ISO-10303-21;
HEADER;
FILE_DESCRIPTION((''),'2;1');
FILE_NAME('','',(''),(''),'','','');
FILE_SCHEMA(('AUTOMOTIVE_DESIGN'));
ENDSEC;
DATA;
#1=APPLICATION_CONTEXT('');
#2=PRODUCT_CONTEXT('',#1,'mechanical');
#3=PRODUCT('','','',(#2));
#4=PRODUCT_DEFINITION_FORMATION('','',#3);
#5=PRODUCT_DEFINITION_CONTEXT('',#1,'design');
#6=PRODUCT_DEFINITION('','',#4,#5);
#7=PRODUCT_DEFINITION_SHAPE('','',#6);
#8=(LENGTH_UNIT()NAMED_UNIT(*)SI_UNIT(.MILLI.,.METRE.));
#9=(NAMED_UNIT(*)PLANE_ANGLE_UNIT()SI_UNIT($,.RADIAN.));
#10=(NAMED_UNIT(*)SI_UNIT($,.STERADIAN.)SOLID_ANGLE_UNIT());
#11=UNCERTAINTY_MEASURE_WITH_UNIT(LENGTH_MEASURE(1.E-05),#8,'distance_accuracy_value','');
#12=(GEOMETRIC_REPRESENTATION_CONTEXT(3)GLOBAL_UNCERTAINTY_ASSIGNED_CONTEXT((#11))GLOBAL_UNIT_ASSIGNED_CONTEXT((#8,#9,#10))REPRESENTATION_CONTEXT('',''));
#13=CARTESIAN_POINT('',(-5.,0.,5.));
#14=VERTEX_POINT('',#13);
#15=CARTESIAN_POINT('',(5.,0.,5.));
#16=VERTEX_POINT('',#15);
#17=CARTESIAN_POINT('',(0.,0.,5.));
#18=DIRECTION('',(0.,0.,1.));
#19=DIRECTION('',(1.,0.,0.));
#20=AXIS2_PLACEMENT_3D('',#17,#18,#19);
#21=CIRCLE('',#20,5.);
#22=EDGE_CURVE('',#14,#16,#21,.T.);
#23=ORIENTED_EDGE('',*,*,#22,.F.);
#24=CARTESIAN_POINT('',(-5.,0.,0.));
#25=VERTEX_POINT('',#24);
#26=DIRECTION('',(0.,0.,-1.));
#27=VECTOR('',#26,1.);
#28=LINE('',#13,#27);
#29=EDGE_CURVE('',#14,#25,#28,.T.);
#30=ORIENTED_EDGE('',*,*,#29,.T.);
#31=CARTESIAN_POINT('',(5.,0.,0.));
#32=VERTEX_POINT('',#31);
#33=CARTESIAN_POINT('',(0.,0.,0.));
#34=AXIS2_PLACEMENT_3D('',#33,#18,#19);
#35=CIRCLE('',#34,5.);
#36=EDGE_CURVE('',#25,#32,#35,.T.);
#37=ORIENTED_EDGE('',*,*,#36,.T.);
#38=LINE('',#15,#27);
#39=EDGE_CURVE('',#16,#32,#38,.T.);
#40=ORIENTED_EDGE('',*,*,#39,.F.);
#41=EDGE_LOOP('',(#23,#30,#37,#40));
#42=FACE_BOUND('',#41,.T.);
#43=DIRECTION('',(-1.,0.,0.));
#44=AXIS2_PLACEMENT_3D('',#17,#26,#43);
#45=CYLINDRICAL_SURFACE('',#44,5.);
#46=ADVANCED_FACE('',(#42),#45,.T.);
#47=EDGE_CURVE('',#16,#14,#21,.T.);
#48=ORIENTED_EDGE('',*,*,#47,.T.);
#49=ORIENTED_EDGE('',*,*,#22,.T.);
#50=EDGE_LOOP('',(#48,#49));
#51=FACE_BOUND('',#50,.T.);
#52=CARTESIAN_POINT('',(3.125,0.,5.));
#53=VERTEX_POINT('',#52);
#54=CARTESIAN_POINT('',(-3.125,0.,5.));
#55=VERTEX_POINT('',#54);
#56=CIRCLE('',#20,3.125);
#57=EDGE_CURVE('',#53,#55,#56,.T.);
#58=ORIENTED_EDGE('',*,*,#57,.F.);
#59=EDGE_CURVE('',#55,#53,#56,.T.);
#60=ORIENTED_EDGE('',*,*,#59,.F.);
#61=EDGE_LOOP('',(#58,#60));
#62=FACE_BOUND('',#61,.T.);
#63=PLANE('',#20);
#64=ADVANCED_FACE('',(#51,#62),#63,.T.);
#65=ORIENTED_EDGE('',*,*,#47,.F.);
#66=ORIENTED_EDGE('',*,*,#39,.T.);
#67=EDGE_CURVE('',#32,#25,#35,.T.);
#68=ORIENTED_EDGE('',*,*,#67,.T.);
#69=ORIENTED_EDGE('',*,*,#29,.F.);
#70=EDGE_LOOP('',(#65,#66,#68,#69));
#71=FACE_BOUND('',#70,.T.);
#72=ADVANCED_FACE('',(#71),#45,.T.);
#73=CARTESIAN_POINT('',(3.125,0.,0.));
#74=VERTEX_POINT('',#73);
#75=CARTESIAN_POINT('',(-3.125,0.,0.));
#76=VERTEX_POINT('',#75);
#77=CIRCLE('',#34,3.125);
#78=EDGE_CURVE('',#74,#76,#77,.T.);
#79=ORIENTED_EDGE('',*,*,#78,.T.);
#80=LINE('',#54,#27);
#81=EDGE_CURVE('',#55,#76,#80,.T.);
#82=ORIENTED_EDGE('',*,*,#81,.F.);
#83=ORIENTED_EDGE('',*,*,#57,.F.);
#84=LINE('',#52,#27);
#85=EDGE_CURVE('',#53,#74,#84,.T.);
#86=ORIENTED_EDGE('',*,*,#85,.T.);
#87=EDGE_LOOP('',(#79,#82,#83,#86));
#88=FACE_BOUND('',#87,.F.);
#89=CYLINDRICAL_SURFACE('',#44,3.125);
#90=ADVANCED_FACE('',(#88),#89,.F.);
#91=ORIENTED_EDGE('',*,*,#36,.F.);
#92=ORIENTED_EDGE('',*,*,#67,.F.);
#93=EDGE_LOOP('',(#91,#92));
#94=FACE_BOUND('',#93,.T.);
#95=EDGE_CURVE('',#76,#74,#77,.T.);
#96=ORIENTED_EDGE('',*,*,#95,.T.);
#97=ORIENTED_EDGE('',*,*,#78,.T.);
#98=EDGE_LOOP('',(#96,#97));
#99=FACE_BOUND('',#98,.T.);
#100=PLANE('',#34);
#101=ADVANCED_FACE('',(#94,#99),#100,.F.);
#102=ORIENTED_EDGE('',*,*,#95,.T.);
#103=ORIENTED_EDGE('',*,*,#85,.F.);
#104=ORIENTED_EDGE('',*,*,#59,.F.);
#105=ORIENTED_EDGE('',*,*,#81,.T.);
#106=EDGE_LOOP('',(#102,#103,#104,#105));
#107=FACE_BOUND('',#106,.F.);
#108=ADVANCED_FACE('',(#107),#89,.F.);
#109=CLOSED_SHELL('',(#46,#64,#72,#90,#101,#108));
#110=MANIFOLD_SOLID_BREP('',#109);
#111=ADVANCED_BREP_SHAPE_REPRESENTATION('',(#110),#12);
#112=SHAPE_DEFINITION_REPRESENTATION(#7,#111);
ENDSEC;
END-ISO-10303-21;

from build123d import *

# Parameters (mm, degrees)
SKETCH1_R           = 5
SKETCH1_R_2         = 3.125
BOSS_EXTRUDE1_DEPTH = 5


with BuildPart() as part:
    # Sketch1 → Boss-Extrude1 (new body)
    with BuildSketch(Plane.XY):
        Circle(SKETCH1_R)
        Circle(SKETCH1_R_2, mode=Mode.SUBTRACT)
    extrude(amount=BOSS_EXTRUDE1_DEPTH)


solid = part.part
